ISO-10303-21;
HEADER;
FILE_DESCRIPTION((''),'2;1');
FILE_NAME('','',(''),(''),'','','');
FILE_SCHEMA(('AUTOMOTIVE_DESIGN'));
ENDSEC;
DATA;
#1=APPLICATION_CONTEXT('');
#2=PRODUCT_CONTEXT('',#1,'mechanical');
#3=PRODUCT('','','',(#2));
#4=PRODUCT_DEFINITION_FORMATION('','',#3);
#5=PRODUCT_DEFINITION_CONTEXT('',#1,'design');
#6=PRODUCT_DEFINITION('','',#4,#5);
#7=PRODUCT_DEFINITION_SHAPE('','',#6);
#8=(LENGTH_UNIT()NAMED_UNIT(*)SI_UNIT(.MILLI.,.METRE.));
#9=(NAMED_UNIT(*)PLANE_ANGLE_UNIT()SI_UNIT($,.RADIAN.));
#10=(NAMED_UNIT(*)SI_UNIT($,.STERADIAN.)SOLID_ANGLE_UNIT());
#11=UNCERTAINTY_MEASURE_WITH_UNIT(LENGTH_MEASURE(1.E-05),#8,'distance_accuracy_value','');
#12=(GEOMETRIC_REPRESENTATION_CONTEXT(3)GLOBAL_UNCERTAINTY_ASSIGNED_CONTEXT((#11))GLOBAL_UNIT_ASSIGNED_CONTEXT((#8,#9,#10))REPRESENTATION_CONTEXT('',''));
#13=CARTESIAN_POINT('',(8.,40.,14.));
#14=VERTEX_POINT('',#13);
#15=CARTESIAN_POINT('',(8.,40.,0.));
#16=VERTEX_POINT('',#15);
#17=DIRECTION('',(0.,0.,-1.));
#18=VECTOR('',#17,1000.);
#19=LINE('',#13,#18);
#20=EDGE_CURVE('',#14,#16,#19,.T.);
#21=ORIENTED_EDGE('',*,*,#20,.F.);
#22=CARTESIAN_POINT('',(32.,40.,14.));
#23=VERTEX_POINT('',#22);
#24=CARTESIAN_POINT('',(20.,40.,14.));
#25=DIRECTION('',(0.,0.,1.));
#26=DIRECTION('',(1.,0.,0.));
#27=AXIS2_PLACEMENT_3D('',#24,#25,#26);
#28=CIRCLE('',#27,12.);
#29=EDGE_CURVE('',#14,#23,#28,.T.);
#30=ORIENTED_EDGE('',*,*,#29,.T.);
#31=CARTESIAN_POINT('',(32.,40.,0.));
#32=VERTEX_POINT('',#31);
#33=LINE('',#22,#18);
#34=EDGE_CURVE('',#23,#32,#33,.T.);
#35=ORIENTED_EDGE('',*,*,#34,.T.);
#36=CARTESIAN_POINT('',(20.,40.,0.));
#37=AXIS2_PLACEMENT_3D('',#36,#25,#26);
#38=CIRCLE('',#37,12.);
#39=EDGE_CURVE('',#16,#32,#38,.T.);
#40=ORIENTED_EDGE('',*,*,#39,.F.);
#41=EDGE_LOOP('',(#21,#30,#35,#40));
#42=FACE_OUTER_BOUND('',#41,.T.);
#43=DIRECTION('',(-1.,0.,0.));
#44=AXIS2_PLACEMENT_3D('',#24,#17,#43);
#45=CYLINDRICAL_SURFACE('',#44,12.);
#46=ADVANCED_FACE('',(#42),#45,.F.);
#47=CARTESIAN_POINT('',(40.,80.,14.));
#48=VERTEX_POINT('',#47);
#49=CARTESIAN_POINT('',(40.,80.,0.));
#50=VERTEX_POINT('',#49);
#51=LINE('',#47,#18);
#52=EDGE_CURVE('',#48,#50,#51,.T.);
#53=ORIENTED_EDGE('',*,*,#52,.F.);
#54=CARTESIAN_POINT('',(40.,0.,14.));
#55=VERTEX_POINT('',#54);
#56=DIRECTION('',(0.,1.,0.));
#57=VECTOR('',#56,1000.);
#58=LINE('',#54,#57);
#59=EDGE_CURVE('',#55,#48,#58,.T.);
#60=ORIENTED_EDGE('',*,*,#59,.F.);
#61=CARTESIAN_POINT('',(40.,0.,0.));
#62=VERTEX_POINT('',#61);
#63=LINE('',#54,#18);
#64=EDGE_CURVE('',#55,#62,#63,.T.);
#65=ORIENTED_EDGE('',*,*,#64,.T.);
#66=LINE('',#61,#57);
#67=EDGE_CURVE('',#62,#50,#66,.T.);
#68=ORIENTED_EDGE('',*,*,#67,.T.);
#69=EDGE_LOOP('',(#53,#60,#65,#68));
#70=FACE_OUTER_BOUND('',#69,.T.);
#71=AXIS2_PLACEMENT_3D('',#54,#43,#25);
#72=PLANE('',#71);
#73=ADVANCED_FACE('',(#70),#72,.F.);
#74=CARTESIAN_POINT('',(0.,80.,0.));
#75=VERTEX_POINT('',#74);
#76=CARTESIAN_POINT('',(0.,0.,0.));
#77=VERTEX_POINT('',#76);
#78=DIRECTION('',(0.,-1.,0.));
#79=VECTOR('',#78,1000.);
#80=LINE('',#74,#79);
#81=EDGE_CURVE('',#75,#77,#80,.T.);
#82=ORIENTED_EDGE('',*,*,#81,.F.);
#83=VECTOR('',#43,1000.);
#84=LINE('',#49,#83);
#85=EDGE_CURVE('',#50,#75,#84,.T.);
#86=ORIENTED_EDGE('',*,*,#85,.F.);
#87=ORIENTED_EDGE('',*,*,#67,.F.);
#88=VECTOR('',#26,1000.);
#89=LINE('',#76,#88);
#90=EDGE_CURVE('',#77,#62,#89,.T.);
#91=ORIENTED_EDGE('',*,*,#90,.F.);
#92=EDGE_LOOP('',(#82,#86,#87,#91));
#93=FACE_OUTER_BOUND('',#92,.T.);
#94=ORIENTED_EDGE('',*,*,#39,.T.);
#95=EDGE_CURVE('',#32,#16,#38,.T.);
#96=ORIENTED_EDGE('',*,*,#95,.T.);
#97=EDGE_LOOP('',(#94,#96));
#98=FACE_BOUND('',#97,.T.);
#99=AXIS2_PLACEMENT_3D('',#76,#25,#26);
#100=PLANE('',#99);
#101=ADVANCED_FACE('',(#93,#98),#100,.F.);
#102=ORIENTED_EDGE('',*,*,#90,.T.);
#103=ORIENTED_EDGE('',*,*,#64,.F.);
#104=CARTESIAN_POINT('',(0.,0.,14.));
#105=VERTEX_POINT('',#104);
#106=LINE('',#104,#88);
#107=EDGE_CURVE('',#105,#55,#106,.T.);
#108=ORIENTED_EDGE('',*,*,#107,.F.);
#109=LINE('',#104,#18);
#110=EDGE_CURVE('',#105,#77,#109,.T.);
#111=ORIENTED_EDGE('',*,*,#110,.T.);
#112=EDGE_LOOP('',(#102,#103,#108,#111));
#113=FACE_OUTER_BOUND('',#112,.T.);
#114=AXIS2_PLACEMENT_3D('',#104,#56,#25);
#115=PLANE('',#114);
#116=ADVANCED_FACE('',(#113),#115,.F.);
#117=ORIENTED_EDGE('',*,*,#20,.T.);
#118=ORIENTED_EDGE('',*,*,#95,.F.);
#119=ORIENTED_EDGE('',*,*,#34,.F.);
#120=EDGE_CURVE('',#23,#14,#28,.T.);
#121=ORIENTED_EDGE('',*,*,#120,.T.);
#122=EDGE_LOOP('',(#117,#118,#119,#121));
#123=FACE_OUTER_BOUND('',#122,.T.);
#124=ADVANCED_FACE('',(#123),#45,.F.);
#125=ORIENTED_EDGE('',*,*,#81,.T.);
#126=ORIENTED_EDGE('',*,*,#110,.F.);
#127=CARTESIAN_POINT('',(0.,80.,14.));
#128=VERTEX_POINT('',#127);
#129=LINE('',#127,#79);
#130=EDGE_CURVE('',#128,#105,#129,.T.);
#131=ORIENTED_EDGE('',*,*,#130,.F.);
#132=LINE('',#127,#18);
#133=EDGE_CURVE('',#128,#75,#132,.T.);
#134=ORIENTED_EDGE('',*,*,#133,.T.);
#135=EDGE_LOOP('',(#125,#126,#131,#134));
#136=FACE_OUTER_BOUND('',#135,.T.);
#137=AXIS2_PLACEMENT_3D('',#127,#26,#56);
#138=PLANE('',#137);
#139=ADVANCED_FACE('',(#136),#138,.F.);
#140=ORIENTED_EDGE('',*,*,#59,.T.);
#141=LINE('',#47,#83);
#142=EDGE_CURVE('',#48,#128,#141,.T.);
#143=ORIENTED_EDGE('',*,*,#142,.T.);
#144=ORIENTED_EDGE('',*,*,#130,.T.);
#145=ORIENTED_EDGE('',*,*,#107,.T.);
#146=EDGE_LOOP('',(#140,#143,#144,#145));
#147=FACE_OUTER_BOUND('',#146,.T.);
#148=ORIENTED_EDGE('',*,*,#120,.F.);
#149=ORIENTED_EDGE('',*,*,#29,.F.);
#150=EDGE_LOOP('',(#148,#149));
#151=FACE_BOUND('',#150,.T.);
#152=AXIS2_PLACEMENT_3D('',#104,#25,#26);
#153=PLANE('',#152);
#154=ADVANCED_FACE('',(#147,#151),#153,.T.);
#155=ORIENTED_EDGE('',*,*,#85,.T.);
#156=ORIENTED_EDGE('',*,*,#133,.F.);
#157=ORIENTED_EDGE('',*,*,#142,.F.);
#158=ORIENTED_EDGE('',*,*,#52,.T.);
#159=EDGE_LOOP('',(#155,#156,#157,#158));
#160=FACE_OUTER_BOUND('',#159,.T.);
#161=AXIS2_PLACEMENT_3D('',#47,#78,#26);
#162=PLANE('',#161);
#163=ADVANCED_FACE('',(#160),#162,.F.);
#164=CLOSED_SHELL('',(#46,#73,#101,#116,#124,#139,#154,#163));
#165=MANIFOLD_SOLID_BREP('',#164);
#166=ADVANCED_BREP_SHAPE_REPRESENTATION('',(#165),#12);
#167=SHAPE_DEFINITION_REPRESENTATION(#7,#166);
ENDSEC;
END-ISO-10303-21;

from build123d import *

# Parameters (mm, degrees)
SKETCH1_W           = 40
SKETCH1_H           = 80
SKETCH1_R           = 12
BOSS_EXTRUDE1_DEPTH = 14


with BuildPart() as part:
    # Sketch1 → Boss-Extrude1 (new body)
    with BuildSketch(Plane.XY):
        with Locations((20, 40)):
            Rectangle(SKETCH1_W, SKETCH1_H)
        with Locations((20, 40)):
            Circle(SKETCH1_R, mode=Mode.SUBTRACT)
    extrude(amount=BOSS_EXTRUDE1_DEPTH)


solid = part.part
